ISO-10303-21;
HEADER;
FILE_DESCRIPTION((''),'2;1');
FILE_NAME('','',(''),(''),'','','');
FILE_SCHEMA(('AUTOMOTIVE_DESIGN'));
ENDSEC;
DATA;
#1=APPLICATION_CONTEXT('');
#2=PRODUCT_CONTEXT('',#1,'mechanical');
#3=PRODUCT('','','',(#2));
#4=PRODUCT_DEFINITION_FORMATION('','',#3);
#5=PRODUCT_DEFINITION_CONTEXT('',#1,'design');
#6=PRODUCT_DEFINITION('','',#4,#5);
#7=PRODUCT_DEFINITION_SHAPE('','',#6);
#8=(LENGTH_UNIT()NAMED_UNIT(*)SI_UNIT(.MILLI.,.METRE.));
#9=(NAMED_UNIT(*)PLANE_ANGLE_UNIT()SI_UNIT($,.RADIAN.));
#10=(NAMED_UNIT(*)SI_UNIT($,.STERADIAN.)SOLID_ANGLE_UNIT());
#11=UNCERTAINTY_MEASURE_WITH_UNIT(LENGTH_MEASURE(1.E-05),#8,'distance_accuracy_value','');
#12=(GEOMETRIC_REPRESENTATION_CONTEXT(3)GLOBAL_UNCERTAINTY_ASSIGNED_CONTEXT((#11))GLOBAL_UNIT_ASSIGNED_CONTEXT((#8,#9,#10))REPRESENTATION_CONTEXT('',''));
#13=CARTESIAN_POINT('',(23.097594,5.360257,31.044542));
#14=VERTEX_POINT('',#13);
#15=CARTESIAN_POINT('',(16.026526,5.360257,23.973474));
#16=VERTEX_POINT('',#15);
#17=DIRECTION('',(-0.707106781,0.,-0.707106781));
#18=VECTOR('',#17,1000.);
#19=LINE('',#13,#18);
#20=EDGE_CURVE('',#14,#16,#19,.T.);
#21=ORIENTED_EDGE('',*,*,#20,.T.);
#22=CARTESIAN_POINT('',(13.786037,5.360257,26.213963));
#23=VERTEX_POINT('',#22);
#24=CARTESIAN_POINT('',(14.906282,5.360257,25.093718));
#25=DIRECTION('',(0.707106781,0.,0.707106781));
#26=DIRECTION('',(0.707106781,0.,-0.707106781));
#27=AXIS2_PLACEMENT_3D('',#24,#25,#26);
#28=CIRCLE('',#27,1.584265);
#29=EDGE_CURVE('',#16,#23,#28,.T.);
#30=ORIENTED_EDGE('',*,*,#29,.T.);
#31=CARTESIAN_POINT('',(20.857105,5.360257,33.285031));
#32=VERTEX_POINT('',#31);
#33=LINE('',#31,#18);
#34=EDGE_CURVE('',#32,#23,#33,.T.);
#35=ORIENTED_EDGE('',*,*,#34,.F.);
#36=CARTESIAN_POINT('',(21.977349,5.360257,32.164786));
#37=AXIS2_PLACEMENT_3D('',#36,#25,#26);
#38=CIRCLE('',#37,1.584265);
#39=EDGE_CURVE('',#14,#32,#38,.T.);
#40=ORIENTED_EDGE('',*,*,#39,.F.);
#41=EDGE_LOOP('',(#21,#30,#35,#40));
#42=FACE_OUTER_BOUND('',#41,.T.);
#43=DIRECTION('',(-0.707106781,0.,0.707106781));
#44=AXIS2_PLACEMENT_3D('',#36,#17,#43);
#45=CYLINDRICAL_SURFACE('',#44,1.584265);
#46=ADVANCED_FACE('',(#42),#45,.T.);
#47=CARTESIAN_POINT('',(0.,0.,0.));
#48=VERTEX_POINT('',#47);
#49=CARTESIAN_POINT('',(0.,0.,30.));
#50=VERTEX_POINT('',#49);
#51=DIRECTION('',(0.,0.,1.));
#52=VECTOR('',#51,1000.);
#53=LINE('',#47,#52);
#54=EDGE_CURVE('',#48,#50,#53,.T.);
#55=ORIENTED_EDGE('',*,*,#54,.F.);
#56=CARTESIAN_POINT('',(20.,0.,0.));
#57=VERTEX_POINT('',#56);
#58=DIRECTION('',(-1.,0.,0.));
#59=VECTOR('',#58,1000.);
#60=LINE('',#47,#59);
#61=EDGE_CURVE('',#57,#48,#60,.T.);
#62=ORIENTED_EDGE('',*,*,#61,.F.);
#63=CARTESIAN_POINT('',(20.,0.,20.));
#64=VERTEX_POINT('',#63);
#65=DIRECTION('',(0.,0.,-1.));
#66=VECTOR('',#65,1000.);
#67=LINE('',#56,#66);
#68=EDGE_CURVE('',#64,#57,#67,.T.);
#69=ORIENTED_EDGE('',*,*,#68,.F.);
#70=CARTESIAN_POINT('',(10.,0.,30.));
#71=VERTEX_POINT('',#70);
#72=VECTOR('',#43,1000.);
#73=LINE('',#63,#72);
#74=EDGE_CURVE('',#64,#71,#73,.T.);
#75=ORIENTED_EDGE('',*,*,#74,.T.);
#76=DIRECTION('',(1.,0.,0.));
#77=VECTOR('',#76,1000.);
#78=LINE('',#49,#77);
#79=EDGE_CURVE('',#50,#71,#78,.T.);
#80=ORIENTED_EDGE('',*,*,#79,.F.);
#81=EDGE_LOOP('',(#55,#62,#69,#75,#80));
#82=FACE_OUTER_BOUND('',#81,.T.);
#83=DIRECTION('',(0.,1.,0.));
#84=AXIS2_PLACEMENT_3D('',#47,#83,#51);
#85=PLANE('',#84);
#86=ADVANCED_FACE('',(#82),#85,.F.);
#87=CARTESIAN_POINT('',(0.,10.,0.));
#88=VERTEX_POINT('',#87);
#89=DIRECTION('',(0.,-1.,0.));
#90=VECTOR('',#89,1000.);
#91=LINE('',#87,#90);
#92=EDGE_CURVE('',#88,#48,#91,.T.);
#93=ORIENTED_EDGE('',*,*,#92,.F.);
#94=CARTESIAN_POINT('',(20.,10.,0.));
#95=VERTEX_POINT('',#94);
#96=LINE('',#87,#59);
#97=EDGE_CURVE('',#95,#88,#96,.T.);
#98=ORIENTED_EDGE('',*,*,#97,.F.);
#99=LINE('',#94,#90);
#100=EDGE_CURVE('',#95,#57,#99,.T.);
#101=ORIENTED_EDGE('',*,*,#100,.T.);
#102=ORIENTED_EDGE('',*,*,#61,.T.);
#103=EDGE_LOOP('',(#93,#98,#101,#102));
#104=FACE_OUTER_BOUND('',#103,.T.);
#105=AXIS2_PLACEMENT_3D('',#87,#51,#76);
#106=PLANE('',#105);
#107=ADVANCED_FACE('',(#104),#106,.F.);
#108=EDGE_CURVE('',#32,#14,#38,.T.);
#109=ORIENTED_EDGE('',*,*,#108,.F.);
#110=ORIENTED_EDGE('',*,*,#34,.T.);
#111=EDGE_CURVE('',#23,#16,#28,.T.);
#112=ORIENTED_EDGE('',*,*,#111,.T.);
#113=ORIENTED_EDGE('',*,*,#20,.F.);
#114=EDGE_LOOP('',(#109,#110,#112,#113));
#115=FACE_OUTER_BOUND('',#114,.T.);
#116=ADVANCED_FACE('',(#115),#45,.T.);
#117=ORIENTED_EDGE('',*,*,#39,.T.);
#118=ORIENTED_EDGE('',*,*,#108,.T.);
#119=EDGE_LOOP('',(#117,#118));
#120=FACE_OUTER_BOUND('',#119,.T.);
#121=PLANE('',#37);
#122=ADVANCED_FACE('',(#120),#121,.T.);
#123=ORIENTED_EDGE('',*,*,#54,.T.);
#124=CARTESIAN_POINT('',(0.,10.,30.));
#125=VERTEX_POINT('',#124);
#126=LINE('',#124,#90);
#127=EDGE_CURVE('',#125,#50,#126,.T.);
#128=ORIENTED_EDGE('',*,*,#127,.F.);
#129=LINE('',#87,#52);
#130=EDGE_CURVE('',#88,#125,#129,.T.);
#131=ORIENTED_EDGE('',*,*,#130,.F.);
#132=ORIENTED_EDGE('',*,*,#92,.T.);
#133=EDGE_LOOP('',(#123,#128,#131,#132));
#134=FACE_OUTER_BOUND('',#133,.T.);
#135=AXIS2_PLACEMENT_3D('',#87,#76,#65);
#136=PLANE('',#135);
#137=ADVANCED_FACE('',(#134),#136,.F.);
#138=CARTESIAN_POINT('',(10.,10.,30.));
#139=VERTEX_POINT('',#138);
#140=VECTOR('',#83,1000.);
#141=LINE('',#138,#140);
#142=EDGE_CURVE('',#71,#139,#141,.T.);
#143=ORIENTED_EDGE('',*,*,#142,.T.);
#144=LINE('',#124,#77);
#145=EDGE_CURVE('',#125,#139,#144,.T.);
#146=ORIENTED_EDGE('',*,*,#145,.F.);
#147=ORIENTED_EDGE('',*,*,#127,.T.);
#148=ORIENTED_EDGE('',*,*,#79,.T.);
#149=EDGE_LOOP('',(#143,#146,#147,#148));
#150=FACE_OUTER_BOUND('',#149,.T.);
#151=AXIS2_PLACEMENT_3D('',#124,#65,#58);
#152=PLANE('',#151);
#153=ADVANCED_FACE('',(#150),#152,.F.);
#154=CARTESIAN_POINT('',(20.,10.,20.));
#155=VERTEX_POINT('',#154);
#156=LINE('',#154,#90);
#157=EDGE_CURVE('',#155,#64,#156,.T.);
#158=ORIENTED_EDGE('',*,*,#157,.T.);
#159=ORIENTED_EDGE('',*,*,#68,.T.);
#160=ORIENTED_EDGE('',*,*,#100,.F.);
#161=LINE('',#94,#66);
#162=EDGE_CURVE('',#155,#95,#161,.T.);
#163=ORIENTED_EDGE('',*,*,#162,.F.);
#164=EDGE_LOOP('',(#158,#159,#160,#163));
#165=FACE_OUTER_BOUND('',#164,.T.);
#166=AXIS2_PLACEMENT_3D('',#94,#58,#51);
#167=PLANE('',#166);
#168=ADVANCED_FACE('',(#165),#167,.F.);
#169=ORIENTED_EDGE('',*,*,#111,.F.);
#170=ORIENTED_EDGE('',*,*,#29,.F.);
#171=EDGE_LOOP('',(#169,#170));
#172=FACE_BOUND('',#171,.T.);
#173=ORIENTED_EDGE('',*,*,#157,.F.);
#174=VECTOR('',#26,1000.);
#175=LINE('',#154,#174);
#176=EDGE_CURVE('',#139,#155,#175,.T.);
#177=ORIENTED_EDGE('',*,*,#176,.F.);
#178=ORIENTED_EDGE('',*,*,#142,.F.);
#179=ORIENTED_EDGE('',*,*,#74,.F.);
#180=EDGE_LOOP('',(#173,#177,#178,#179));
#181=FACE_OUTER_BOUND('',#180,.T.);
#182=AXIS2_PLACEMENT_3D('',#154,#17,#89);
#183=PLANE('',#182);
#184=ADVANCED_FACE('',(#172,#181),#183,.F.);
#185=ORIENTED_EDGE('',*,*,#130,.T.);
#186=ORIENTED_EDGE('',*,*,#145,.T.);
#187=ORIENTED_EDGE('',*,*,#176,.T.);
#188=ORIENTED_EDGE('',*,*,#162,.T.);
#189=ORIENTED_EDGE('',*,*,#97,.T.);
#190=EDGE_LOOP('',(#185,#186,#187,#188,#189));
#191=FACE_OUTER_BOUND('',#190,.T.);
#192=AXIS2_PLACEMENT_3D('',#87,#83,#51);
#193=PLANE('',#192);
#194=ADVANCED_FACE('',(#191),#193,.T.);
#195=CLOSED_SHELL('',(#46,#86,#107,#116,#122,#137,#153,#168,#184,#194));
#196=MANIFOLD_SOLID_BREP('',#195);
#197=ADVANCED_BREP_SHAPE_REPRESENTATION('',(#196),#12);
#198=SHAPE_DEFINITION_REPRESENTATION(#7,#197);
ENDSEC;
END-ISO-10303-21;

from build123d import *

# Parameters (mm, degrees)
SKETCH1_W           = 20
SKETCH1_H           = 30
BOSS_EXTRUDE1_DEPTH = 10
CHAMFER1_SIZE       = 10
SKETCH2_R           = 1.584264685
BOSS_EXTRUDE2_DEPTH = 10


with BuildPart() as part:
    # Sketch1 → Boss-Extrude1 (new body)
    with BuildSketch(Plane(origin=(0, 0, 0), x_dir=(1, 0, 0), z_dir=(0, 1, 0))):
        with Locations((10, -15)):
            Rectangle(SKETCH1_W, SKETCH1_H)
    extrude(amount=BOSS_EXTRUDE1_DEPTH)

    # Chamfer1
    chamfer1_edges = [part.edges().sort_by_distance(p)[0] for p in [
        (20, 5, 30),
    ]]
    chamfer(chamfer1_edges, length=CHAMFER1_SIZE)

    # Sketch2 → Boss-Extrude2 (add)
    with BuildSketch(Plane(origin=(20, 0, 20), x_dir=(0.7071067811865487, 0, -0.7071067811865465), z_dir=(0.7071067811865465, 0, 0.7071067811865487))):
        with Locations((-7.203605768, 5.360257058)):
            Circle(SKETCH2_R)
    extrude(amount=BOSS_EXTRUDE2_DEPTH)


solid = part.part
